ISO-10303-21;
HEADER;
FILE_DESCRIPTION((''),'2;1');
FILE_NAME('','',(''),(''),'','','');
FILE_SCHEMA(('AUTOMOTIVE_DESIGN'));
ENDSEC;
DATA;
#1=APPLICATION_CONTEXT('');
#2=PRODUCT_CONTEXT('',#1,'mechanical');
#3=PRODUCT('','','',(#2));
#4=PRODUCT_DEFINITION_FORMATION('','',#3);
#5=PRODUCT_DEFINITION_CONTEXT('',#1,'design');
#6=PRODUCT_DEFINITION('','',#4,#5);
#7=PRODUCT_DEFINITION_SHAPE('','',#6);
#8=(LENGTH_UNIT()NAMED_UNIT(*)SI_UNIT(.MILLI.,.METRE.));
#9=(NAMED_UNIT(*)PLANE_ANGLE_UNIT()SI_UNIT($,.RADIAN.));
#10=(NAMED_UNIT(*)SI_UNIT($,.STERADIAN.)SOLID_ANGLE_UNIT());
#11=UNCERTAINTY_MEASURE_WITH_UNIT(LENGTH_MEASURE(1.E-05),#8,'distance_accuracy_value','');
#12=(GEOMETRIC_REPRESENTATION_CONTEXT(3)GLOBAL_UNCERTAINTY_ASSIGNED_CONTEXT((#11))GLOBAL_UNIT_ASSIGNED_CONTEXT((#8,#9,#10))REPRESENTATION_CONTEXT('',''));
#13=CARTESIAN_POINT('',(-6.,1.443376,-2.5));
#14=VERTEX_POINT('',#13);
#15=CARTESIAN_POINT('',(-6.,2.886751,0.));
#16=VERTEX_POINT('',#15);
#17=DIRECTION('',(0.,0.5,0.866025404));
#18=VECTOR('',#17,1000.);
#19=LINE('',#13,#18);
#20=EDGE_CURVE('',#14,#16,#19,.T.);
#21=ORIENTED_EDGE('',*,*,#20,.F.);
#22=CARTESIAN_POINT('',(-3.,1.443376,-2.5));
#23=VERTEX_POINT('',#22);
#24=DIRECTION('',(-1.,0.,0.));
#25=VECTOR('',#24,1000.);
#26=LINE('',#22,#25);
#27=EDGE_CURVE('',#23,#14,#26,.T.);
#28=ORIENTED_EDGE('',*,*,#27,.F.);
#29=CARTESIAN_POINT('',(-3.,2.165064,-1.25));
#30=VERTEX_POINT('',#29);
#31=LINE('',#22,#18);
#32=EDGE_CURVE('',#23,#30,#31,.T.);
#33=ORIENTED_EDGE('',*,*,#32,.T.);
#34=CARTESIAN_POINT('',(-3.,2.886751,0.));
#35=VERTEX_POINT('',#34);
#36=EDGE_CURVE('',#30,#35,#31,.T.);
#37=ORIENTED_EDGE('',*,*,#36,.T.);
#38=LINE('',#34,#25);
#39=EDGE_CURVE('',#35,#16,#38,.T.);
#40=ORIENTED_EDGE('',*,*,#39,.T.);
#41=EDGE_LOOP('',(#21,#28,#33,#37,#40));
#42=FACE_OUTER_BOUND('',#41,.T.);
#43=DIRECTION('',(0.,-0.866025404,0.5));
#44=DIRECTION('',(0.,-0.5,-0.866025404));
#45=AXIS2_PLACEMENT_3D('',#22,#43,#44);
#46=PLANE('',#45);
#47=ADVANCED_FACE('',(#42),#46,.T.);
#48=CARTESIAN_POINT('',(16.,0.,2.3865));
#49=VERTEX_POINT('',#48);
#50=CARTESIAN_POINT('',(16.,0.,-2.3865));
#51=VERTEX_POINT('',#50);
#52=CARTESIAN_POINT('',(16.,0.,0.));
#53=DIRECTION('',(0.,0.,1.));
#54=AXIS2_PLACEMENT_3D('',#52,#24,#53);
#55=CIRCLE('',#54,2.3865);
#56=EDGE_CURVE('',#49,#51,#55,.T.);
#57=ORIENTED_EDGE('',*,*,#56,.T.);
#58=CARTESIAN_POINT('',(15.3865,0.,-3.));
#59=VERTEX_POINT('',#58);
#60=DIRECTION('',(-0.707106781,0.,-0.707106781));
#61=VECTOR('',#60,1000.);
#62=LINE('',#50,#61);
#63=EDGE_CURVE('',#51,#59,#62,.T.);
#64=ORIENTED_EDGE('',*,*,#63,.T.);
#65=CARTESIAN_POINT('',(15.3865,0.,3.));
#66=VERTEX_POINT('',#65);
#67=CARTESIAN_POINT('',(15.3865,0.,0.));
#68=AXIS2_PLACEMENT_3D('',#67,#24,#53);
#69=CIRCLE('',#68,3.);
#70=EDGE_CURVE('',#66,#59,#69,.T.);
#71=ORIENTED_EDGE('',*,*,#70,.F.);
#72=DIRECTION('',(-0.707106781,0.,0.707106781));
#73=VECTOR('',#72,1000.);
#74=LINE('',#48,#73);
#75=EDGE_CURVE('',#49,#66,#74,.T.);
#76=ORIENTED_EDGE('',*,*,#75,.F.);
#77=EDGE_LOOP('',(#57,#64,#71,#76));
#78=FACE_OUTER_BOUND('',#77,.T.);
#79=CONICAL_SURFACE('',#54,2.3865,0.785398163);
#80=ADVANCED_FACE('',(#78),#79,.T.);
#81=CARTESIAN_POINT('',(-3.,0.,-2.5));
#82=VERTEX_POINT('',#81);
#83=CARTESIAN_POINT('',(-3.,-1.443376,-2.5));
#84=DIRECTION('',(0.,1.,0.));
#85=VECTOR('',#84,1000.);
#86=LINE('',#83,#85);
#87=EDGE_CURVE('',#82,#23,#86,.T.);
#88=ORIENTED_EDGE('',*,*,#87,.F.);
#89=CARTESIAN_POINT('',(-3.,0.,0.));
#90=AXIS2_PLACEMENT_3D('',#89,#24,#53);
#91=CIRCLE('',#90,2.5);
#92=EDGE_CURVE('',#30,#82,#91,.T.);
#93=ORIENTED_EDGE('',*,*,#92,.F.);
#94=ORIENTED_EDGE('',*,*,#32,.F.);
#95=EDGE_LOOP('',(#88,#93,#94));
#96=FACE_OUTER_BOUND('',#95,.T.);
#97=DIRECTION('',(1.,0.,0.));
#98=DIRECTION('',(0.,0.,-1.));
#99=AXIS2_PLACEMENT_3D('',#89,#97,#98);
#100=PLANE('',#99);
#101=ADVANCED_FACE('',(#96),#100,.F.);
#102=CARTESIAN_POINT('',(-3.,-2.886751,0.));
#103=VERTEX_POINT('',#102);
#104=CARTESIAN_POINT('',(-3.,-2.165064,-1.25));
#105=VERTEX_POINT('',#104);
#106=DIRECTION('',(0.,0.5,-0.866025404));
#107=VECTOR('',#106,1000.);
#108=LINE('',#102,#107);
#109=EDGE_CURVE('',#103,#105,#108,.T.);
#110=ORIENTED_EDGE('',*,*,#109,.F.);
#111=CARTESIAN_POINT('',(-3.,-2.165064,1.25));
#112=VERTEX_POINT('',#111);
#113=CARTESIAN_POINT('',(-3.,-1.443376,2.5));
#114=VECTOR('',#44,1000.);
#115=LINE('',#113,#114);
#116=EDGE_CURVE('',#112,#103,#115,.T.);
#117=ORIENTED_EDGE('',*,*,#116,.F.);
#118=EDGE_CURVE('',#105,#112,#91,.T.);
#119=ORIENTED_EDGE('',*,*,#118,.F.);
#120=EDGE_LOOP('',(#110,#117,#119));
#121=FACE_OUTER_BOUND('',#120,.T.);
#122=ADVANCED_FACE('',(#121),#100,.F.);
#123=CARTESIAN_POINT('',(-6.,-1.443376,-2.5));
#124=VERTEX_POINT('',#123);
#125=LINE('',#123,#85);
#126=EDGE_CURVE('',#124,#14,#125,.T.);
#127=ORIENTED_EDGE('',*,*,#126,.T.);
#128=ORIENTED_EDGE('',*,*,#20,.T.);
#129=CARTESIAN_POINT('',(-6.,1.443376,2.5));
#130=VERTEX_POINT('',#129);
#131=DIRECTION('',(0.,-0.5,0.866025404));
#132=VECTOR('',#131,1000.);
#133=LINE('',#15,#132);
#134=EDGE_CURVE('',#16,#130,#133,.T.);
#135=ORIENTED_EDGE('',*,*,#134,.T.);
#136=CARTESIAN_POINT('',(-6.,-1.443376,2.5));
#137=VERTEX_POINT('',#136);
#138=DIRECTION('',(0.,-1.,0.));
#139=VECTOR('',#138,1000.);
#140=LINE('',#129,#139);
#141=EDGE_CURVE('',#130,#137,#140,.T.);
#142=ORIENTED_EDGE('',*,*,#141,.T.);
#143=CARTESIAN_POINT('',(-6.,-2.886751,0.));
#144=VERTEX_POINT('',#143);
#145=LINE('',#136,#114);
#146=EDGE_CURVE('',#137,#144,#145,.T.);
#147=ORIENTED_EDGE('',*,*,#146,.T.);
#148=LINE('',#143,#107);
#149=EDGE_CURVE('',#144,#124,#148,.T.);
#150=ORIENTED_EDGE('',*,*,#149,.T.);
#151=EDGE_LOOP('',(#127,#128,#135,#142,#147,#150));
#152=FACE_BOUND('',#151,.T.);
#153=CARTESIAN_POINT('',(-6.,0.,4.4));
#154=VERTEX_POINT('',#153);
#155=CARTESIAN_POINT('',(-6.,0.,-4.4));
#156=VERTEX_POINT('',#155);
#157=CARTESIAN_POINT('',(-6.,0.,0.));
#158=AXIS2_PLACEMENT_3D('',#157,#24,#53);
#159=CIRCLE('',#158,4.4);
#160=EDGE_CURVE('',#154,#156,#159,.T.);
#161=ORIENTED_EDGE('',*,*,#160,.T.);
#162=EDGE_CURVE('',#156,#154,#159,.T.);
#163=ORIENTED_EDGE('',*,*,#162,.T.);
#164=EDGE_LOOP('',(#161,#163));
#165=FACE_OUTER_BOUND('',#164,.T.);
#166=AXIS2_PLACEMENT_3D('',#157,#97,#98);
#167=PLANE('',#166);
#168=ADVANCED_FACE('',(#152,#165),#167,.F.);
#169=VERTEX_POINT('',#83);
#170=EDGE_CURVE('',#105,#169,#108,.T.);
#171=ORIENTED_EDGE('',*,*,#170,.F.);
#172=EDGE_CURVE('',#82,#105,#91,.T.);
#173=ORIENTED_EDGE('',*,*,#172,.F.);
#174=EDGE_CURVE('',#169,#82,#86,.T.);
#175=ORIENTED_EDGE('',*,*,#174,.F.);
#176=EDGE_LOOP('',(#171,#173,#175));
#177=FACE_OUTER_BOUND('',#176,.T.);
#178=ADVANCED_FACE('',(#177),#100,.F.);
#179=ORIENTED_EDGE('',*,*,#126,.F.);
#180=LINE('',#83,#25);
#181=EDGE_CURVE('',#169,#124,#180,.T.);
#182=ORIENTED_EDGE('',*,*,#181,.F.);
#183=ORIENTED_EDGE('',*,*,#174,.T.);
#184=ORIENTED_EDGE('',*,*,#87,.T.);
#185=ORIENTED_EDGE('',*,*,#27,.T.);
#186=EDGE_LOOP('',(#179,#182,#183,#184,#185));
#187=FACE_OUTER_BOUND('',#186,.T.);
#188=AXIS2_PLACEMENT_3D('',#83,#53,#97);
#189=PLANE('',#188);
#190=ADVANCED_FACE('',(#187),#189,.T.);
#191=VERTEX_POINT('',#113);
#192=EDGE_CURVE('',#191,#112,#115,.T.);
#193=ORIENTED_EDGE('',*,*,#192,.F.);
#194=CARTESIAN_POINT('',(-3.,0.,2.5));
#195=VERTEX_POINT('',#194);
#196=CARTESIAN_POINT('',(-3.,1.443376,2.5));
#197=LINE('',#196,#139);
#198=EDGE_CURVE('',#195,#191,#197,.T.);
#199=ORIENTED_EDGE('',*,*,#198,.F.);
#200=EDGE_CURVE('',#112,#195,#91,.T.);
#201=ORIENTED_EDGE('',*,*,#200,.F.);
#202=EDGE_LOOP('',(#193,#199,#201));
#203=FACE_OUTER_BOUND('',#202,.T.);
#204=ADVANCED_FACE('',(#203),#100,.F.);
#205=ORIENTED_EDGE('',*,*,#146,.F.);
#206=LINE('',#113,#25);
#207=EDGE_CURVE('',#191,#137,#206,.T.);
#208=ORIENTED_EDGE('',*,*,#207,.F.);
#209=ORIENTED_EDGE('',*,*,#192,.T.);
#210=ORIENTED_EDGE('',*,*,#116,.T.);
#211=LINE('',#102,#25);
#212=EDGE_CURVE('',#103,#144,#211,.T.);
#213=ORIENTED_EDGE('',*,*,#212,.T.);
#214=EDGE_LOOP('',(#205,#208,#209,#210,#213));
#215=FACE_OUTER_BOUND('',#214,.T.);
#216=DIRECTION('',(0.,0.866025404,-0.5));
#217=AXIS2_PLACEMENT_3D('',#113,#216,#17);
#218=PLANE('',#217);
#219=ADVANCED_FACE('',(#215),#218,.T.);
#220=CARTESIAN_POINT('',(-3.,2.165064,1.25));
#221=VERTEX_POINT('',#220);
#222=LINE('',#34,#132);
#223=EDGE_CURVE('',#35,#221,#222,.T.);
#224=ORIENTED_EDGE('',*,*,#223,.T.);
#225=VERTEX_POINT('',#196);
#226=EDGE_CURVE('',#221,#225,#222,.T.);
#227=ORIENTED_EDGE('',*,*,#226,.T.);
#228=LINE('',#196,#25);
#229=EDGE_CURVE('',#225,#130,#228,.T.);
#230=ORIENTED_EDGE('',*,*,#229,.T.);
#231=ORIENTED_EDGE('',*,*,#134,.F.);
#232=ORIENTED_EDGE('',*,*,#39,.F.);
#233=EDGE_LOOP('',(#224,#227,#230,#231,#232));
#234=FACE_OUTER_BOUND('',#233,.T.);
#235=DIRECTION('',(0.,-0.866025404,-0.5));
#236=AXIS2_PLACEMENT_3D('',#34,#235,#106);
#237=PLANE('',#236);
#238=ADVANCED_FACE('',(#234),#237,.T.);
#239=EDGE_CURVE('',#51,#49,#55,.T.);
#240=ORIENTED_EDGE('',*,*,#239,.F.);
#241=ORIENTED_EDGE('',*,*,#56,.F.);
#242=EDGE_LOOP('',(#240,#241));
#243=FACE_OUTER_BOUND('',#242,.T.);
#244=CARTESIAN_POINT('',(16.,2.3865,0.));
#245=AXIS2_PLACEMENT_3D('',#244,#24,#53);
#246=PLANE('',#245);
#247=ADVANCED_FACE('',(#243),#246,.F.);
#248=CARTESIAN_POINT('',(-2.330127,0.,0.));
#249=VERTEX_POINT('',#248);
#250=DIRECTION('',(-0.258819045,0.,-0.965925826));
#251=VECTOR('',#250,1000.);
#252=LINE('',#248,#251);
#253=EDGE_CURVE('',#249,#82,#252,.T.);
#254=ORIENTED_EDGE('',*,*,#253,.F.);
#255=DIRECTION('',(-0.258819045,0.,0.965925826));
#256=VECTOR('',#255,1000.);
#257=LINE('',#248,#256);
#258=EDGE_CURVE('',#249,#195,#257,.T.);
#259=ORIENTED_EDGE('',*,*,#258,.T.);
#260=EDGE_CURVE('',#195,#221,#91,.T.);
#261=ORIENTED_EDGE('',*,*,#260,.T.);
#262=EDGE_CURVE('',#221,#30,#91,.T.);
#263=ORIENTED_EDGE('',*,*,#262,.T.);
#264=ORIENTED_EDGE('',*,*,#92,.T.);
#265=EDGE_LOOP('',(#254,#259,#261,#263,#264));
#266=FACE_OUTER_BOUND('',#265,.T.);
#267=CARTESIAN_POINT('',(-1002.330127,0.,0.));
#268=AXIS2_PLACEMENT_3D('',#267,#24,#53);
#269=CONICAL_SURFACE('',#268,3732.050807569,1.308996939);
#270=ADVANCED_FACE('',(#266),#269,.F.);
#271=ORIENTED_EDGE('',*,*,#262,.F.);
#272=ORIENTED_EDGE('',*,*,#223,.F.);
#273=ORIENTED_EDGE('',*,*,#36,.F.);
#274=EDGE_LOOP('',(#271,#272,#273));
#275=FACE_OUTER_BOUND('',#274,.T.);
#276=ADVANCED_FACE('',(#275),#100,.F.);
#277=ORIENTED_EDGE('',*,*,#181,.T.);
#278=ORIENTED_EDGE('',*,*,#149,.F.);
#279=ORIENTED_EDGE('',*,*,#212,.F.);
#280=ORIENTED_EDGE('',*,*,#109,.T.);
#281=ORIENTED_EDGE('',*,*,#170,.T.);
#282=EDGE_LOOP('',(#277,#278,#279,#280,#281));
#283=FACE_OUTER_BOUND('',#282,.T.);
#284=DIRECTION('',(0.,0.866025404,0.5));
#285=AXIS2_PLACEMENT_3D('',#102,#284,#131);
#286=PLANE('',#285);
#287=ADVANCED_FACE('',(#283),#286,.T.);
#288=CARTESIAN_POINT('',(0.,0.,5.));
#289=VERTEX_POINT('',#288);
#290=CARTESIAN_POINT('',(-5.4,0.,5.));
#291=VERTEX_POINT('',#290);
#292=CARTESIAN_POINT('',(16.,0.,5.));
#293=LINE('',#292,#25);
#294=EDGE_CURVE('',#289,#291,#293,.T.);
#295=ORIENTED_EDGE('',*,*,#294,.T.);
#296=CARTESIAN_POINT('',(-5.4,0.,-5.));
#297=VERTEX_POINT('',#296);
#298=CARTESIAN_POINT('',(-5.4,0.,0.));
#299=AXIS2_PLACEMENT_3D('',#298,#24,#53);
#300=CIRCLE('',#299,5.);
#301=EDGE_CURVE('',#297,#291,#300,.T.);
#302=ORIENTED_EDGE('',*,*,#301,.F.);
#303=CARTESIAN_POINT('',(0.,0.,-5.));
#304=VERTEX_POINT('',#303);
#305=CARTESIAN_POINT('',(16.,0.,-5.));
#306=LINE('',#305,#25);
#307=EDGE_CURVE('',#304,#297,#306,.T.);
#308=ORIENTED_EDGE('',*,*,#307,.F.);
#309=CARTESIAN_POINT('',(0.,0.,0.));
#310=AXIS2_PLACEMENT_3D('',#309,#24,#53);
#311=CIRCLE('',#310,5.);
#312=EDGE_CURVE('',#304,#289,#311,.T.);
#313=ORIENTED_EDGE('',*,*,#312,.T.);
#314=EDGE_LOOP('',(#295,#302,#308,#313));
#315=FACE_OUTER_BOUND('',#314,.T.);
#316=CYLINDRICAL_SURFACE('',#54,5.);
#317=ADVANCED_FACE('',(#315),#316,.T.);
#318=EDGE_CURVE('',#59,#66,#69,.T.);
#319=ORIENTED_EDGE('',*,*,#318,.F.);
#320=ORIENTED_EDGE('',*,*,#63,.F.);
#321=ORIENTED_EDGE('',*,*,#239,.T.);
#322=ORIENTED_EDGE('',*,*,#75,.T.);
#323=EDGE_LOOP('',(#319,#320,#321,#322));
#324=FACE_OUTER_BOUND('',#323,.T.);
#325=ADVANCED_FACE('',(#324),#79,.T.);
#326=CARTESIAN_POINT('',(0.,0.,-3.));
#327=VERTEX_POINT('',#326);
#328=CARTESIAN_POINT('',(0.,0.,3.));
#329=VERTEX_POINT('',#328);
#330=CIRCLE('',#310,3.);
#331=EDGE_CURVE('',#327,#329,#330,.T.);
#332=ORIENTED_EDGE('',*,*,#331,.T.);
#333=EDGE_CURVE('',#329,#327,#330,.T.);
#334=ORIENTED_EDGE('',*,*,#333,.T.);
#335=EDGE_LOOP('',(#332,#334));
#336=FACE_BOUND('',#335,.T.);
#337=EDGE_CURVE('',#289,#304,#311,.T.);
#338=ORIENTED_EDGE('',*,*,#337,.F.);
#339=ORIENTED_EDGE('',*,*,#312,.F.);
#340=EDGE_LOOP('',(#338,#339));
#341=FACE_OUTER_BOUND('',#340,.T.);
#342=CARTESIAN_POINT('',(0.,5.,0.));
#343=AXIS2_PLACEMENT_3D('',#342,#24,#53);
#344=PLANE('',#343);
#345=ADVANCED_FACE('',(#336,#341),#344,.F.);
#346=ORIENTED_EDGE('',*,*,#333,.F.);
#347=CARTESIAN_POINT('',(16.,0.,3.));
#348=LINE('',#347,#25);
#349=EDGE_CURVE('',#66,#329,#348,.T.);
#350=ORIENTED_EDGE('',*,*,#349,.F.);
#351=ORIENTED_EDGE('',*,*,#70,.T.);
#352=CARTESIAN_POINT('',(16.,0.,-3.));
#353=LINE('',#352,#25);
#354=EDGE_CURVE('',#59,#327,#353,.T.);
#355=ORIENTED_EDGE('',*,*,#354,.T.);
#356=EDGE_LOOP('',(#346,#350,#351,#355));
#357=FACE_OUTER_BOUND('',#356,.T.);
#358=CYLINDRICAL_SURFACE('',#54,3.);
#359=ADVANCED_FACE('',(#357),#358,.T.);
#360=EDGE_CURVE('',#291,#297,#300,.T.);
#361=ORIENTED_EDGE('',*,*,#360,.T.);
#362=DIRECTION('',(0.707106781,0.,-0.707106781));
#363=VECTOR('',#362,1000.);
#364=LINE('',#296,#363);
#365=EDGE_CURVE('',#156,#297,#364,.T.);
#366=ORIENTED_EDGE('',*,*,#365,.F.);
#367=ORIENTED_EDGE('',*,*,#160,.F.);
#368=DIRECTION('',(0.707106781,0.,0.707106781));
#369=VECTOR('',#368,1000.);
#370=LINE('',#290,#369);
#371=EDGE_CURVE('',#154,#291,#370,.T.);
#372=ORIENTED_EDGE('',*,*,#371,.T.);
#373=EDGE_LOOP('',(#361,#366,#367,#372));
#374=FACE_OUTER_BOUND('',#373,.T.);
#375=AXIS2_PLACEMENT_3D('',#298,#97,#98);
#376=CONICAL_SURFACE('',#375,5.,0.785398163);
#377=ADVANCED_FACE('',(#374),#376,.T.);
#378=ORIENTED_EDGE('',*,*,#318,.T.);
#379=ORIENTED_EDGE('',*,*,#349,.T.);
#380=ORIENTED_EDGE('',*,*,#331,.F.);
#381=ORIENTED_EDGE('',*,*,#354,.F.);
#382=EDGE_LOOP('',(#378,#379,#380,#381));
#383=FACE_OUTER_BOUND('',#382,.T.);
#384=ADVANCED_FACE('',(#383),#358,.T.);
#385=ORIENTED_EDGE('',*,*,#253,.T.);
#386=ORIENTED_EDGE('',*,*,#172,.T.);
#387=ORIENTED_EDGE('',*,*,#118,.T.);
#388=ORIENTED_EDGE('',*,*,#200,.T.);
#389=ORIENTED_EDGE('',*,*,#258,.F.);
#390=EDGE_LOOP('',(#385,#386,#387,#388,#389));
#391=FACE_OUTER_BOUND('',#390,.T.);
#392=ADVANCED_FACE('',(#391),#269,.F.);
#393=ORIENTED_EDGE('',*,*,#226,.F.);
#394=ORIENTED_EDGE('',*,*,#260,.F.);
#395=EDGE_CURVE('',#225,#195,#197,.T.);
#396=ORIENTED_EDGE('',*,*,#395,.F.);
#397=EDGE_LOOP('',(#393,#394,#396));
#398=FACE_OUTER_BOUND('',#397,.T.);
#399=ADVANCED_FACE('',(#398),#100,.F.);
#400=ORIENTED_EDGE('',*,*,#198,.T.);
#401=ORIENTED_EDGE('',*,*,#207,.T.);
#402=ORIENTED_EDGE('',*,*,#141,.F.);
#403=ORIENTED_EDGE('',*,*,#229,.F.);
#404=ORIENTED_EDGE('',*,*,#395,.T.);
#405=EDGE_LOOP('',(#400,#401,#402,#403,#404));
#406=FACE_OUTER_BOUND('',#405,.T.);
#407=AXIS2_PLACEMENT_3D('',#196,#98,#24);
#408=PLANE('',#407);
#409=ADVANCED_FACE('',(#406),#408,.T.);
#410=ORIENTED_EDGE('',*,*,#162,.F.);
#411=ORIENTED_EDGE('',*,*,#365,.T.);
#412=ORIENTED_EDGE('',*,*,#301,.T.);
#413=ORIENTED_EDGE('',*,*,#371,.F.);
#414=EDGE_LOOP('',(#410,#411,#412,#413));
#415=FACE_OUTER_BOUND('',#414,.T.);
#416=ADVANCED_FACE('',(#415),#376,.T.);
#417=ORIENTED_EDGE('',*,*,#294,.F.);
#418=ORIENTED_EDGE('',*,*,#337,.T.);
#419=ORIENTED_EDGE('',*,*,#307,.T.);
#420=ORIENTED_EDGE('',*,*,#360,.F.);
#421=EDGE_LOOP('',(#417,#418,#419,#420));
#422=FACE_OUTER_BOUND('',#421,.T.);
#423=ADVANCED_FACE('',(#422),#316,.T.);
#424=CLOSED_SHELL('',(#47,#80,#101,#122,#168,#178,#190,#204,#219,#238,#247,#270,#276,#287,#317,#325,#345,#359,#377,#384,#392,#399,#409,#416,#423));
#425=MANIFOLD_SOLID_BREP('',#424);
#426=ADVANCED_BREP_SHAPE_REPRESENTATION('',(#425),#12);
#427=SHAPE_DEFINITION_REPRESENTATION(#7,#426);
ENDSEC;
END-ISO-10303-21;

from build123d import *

# Parameters (mm, degrees)
CUT_EXTRUDE_1_DEPTH = 3


with BuildPart() as part:
    # 草图1 → 旋转1 (revolve)
    with BuildSketch(Plane.XY, mode=Mode.PRIVATE) as revolve_1_sk:
        Polygon((-6, 0), (-6, 4.4), (-5.4, 5), (0, 5), (0, 3), (15.3865, 3), (16, 2.3865), (16, 0), align=None)
    revolve(revolve_1_sk.sketch.rotate(Axis((16, 0, 0), (-1, 0, 0)), 270), axis=Axis((16, 0, 0), (-1, 0, 0)))

    # 草图2 → 切除-旋转1 (revolve, cut)
    with BuildSketch(Plane.XY, mode=Mode.PRIVATE) as cut_revolve_1_sk:
        Polygon((-6, 0), (-6, 2.5), (-3, 2.5), (-2.330127019, 0), align=None)
    revolve(cut_revolve_1_sk.sketch.rotate(Axis((-2.330127019, 0, 0), (-1, 0, 0)), 270), axis=Axis((-2.330127019, 0, 0), (-1, 0, 0)), mode=Mode.SUBTRACT)

    # 草图3 → 切除-拉伸1 (cut)
    with BuildSketch(Plane(origin=(-6, 0, 0), x_dir=(0, 0, -1), z_dir=(1, 0, 0))):
        Polygon((-2.5, 1.443375673), (-2.5, -1.443375673), (0, -2.886751346), (2.5, -1.443375673), (2.5, 1.443375673), (0, 2.886751346), align=None)
    extrude(amount=CUT_EXTRUDE_1_DEPTH, mode=Mode.SUBTRACT)


solid = part.part
